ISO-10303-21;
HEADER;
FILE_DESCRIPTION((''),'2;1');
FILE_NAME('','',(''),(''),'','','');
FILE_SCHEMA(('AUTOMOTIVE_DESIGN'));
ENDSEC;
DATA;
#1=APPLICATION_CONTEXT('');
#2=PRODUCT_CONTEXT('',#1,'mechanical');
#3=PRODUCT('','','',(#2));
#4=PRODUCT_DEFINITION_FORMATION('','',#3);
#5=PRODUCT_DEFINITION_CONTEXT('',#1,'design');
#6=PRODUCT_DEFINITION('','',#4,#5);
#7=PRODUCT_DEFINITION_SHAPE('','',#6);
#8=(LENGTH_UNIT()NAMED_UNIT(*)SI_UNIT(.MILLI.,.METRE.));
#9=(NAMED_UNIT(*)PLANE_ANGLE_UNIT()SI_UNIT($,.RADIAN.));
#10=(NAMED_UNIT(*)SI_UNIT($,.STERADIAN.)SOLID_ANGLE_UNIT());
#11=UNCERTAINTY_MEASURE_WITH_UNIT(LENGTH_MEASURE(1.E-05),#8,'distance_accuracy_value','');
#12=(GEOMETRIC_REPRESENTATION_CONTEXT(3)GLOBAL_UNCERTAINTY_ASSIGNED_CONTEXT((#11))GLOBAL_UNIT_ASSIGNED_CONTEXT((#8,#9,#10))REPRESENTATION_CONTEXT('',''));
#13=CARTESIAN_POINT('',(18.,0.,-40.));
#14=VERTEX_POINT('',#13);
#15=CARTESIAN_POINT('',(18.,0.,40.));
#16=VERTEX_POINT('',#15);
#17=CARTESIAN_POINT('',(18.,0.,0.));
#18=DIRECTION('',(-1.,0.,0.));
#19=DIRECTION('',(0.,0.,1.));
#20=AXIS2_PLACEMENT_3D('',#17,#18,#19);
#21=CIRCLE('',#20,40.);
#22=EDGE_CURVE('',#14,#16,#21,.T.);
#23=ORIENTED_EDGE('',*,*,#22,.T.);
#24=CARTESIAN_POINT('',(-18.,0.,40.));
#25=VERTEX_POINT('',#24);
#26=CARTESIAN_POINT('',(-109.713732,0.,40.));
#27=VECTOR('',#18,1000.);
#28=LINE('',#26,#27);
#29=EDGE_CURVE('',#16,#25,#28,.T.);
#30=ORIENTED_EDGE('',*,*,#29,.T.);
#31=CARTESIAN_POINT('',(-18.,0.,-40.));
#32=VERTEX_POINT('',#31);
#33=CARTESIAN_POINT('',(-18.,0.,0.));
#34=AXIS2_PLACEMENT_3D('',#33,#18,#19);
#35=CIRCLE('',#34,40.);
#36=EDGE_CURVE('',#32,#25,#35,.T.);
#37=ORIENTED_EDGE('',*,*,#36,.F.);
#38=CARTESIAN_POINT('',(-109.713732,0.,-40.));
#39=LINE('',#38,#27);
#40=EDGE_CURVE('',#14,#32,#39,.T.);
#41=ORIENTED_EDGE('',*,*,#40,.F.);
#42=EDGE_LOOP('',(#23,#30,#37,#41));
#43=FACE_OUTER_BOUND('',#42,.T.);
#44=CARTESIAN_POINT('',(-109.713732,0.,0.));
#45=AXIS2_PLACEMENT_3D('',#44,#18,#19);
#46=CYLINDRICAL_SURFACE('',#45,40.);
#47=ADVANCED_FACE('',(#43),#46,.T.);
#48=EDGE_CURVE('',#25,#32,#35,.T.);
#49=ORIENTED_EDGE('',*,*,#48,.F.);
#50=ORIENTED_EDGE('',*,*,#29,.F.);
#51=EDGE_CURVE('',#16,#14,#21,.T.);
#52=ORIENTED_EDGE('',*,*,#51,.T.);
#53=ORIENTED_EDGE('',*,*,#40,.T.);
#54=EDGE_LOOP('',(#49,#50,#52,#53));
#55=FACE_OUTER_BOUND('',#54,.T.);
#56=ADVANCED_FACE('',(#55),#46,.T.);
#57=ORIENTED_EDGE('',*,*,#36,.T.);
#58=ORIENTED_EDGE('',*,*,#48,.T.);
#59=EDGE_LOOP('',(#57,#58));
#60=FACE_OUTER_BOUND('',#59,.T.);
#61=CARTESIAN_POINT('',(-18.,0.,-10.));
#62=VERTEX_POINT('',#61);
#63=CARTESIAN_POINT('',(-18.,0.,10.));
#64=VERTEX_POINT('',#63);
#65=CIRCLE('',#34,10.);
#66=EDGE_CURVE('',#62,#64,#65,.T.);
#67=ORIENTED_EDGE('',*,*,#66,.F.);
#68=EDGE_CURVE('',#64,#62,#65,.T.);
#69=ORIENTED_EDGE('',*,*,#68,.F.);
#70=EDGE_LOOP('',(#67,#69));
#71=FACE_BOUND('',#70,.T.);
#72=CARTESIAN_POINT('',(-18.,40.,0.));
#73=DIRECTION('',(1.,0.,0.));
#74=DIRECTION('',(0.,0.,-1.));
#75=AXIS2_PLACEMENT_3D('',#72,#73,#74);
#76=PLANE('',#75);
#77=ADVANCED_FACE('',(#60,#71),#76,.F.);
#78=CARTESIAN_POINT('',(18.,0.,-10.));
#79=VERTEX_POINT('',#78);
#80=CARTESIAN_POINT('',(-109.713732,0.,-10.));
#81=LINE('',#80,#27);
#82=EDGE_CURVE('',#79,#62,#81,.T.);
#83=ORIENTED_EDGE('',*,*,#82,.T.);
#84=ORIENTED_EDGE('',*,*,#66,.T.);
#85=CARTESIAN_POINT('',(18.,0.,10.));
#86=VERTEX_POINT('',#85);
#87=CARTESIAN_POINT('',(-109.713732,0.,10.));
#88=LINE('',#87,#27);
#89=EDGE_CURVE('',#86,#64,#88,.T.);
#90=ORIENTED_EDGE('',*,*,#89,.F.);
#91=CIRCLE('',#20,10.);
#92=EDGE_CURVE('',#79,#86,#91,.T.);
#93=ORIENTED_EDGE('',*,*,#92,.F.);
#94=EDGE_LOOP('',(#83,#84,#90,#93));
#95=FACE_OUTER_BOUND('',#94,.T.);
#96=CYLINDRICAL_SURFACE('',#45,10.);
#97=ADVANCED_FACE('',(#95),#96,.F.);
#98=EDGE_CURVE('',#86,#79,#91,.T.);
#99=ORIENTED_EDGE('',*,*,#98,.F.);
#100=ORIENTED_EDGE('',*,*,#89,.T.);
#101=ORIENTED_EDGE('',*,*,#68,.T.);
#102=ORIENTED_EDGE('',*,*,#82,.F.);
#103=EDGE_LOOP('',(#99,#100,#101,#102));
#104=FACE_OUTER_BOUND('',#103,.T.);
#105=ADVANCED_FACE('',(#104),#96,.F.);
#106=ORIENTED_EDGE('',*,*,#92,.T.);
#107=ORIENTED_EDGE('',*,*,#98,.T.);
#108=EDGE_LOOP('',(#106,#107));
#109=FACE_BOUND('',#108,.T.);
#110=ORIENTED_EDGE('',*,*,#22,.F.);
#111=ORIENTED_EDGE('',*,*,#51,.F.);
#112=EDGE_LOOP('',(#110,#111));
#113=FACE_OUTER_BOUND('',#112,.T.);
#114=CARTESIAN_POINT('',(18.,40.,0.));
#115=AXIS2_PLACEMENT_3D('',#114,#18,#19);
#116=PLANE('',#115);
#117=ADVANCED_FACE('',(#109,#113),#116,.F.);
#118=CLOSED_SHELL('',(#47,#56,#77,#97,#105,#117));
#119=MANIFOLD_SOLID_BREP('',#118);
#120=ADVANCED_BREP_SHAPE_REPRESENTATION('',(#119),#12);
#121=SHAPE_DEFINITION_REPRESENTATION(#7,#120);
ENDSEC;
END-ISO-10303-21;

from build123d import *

# Parameters (mm, degrees)
SKETCH1_W = 36
SKETCH1_H = 30


with BuildPart() as part:
    # Sketch1 → Revolve1 (revolve)
    with BuildSketch(Plane.XY, mode=Mode.PRIVATE) as revolve1_sk:
        with Locations((0, 25)):
            Rectangle(SKETCH1_W, SKETCH1_H)
    revolve(revolve1_sk.sketch.rotate(Axis((-109.713732369, 0, 0), (1, 0, 0)), 90), axis=Axis((-109.713732369, 0, 0), (1, 0, 0)))


solid = part.part
